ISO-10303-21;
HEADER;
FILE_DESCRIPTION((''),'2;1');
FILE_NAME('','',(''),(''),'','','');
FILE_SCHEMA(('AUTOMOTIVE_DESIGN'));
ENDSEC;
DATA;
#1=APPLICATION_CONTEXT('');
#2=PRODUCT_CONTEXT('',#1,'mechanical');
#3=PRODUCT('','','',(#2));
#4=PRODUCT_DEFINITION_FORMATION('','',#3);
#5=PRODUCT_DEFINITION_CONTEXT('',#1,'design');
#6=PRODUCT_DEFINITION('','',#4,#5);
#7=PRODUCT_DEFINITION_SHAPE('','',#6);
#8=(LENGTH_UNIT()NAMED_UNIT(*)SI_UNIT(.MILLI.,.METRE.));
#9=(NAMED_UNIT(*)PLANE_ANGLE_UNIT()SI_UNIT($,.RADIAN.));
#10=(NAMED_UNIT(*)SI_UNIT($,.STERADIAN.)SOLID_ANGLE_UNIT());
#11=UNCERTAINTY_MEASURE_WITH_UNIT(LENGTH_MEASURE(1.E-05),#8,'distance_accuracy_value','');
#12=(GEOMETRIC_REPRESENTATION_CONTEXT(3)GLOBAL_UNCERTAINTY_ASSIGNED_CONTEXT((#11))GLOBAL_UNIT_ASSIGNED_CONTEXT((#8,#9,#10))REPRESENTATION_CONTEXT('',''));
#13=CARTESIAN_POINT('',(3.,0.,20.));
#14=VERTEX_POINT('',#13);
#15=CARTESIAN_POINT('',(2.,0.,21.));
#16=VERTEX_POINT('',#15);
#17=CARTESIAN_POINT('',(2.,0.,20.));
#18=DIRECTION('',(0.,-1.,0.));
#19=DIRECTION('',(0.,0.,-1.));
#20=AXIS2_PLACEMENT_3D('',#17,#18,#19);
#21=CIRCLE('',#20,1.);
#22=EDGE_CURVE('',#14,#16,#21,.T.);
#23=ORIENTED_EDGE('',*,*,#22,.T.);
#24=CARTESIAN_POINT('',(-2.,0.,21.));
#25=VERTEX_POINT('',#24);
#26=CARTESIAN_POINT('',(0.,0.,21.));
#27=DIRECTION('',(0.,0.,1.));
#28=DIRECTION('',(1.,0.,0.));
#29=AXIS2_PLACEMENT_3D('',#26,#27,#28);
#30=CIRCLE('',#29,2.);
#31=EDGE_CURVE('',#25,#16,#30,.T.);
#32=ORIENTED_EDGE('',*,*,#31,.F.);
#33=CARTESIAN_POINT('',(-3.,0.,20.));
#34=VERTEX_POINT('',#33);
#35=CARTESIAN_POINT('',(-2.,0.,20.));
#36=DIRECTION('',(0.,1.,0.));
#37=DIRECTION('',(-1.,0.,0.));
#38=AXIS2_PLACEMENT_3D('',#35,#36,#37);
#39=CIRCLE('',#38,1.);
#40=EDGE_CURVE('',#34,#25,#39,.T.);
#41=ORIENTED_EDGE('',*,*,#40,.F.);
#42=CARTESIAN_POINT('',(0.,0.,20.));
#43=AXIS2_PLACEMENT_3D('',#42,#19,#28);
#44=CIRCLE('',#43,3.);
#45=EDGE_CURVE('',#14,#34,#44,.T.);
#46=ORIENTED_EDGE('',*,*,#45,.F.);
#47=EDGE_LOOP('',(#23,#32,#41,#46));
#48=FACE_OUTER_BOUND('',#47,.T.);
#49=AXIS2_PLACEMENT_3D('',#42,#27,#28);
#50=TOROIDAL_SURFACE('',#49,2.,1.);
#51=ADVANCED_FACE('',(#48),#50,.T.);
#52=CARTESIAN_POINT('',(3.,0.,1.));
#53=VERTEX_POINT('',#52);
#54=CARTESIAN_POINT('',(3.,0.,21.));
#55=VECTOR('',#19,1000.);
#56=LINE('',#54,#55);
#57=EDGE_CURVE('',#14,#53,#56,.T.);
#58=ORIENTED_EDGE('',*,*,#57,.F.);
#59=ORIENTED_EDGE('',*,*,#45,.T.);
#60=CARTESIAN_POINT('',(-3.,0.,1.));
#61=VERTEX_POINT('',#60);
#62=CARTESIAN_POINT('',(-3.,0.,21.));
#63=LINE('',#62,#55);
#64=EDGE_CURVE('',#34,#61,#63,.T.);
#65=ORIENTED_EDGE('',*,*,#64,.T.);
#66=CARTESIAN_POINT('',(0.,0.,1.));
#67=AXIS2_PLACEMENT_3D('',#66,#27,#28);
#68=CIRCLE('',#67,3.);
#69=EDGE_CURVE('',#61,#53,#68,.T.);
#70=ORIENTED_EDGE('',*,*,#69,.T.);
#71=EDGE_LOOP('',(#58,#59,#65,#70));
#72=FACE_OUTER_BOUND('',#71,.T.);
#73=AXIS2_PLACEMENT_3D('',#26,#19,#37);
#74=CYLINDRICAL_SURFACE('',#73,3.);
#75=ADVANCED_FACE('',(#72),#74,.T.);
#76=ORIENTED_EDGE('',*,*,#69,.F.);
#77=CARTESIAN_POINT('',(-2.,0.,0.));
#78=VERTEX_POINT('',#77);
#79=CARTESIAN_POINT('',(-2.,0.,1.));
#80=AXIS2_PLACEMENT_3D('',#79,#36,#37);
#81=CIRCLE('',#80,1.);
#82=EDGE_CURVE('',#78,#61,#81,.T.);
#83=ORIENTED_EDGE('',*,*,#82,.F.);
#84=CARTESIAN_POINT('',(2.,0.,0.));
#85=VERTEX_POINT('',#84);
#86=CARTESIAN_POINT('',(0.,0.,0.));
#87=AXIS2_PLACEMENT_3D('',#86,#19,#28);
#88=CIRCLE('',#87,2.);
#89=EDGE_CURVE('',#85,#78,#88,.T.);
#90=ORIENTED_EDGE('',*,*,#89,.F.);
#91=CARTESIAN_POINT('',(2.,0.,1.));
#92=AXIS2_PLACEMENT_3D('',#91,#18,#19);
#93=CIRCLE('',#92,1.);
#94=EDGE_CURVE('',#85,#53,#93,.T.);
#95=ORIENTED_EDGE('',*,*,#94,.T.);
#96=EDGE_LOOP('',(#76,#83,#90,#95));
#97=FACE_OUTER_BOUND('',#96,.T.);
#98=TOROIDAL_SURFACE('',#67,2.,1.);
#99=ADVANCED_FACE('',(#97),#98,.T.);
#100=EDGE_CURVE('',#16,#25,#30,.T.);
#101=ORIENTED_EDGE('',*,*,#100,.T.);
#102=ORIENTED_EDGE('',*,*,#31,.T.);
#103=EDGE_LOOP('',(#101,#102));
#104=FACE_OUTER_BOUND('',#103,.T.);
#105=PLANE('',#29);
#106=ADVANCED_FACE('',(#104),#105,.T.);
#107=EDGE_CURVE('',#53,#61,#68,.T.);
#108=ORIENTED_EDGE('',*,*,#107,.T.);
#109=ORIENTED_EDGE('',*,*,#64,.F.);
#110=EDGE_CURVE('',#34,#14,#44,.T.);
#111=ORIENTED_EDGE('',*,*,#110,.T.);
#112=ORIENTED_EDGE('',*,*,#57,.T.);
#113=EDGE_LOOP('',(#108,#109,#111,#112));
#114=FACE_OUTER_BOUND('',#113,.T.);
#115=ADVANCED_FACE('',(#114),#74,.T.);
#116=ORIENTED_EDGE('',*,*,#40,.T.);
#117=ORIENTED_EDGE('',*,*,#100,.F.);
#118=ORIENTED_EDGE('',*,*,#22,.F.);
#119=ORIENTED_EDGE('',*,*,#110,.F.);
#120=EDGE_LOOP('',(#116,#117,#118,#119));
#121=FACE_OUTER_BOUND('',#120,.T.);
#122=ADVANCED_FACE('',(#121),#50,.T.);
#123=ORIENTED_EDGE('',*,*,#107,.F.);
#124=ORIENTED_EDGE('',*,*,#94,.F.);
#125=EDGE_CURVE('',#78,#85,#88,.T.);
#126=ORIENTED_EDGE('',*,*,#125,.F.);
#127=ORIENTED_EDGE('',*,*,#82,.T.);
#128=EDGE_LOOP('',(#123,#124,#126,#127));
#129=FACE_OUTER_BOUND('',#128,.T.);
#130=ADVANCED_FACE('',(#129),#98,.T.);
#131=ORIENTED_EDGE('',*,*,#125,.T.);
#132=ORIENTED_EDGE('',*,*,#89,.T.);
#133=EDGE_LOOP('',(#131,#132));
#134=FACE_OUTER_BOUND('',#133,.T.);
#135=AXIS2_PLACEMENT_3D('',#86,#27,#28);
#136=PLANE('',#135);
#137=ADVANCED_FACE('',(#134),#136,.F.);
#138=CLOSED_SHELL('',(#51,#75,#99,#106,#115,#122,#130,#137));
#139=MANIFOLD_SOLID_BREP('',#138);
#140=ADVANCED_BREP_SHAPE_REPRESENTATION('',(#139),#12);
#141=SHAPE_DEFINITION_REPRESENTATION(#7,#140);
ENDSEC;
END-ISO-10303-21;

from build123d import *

# Parameters (mm, degrees)
SKETCH1_R           = 3
BOSS_EXTRUDE1_DEPTH = 21
FILLET1_R           = 1


with BuildPart() as part:
    # Sketch1 → Boss-Extrude1 (new body)
    with BuildSketch(Plane.XY):
        with Locations(Location((0, 0, 0), (0, 0, 180))):
            Circle(SKETCH1_R)
    extrude(amount=BOSS_EXTRUDE1_DEPTH)

    # Fillet1
    fillet1_edges = [part.edges().sort_by_distance(p)[0] for p in [
        (3, 0, 0),
        (3, 0, 21),
    ]]
    fillet(fillet1_edges, radius=FILLET1_R)


solid = part.part
